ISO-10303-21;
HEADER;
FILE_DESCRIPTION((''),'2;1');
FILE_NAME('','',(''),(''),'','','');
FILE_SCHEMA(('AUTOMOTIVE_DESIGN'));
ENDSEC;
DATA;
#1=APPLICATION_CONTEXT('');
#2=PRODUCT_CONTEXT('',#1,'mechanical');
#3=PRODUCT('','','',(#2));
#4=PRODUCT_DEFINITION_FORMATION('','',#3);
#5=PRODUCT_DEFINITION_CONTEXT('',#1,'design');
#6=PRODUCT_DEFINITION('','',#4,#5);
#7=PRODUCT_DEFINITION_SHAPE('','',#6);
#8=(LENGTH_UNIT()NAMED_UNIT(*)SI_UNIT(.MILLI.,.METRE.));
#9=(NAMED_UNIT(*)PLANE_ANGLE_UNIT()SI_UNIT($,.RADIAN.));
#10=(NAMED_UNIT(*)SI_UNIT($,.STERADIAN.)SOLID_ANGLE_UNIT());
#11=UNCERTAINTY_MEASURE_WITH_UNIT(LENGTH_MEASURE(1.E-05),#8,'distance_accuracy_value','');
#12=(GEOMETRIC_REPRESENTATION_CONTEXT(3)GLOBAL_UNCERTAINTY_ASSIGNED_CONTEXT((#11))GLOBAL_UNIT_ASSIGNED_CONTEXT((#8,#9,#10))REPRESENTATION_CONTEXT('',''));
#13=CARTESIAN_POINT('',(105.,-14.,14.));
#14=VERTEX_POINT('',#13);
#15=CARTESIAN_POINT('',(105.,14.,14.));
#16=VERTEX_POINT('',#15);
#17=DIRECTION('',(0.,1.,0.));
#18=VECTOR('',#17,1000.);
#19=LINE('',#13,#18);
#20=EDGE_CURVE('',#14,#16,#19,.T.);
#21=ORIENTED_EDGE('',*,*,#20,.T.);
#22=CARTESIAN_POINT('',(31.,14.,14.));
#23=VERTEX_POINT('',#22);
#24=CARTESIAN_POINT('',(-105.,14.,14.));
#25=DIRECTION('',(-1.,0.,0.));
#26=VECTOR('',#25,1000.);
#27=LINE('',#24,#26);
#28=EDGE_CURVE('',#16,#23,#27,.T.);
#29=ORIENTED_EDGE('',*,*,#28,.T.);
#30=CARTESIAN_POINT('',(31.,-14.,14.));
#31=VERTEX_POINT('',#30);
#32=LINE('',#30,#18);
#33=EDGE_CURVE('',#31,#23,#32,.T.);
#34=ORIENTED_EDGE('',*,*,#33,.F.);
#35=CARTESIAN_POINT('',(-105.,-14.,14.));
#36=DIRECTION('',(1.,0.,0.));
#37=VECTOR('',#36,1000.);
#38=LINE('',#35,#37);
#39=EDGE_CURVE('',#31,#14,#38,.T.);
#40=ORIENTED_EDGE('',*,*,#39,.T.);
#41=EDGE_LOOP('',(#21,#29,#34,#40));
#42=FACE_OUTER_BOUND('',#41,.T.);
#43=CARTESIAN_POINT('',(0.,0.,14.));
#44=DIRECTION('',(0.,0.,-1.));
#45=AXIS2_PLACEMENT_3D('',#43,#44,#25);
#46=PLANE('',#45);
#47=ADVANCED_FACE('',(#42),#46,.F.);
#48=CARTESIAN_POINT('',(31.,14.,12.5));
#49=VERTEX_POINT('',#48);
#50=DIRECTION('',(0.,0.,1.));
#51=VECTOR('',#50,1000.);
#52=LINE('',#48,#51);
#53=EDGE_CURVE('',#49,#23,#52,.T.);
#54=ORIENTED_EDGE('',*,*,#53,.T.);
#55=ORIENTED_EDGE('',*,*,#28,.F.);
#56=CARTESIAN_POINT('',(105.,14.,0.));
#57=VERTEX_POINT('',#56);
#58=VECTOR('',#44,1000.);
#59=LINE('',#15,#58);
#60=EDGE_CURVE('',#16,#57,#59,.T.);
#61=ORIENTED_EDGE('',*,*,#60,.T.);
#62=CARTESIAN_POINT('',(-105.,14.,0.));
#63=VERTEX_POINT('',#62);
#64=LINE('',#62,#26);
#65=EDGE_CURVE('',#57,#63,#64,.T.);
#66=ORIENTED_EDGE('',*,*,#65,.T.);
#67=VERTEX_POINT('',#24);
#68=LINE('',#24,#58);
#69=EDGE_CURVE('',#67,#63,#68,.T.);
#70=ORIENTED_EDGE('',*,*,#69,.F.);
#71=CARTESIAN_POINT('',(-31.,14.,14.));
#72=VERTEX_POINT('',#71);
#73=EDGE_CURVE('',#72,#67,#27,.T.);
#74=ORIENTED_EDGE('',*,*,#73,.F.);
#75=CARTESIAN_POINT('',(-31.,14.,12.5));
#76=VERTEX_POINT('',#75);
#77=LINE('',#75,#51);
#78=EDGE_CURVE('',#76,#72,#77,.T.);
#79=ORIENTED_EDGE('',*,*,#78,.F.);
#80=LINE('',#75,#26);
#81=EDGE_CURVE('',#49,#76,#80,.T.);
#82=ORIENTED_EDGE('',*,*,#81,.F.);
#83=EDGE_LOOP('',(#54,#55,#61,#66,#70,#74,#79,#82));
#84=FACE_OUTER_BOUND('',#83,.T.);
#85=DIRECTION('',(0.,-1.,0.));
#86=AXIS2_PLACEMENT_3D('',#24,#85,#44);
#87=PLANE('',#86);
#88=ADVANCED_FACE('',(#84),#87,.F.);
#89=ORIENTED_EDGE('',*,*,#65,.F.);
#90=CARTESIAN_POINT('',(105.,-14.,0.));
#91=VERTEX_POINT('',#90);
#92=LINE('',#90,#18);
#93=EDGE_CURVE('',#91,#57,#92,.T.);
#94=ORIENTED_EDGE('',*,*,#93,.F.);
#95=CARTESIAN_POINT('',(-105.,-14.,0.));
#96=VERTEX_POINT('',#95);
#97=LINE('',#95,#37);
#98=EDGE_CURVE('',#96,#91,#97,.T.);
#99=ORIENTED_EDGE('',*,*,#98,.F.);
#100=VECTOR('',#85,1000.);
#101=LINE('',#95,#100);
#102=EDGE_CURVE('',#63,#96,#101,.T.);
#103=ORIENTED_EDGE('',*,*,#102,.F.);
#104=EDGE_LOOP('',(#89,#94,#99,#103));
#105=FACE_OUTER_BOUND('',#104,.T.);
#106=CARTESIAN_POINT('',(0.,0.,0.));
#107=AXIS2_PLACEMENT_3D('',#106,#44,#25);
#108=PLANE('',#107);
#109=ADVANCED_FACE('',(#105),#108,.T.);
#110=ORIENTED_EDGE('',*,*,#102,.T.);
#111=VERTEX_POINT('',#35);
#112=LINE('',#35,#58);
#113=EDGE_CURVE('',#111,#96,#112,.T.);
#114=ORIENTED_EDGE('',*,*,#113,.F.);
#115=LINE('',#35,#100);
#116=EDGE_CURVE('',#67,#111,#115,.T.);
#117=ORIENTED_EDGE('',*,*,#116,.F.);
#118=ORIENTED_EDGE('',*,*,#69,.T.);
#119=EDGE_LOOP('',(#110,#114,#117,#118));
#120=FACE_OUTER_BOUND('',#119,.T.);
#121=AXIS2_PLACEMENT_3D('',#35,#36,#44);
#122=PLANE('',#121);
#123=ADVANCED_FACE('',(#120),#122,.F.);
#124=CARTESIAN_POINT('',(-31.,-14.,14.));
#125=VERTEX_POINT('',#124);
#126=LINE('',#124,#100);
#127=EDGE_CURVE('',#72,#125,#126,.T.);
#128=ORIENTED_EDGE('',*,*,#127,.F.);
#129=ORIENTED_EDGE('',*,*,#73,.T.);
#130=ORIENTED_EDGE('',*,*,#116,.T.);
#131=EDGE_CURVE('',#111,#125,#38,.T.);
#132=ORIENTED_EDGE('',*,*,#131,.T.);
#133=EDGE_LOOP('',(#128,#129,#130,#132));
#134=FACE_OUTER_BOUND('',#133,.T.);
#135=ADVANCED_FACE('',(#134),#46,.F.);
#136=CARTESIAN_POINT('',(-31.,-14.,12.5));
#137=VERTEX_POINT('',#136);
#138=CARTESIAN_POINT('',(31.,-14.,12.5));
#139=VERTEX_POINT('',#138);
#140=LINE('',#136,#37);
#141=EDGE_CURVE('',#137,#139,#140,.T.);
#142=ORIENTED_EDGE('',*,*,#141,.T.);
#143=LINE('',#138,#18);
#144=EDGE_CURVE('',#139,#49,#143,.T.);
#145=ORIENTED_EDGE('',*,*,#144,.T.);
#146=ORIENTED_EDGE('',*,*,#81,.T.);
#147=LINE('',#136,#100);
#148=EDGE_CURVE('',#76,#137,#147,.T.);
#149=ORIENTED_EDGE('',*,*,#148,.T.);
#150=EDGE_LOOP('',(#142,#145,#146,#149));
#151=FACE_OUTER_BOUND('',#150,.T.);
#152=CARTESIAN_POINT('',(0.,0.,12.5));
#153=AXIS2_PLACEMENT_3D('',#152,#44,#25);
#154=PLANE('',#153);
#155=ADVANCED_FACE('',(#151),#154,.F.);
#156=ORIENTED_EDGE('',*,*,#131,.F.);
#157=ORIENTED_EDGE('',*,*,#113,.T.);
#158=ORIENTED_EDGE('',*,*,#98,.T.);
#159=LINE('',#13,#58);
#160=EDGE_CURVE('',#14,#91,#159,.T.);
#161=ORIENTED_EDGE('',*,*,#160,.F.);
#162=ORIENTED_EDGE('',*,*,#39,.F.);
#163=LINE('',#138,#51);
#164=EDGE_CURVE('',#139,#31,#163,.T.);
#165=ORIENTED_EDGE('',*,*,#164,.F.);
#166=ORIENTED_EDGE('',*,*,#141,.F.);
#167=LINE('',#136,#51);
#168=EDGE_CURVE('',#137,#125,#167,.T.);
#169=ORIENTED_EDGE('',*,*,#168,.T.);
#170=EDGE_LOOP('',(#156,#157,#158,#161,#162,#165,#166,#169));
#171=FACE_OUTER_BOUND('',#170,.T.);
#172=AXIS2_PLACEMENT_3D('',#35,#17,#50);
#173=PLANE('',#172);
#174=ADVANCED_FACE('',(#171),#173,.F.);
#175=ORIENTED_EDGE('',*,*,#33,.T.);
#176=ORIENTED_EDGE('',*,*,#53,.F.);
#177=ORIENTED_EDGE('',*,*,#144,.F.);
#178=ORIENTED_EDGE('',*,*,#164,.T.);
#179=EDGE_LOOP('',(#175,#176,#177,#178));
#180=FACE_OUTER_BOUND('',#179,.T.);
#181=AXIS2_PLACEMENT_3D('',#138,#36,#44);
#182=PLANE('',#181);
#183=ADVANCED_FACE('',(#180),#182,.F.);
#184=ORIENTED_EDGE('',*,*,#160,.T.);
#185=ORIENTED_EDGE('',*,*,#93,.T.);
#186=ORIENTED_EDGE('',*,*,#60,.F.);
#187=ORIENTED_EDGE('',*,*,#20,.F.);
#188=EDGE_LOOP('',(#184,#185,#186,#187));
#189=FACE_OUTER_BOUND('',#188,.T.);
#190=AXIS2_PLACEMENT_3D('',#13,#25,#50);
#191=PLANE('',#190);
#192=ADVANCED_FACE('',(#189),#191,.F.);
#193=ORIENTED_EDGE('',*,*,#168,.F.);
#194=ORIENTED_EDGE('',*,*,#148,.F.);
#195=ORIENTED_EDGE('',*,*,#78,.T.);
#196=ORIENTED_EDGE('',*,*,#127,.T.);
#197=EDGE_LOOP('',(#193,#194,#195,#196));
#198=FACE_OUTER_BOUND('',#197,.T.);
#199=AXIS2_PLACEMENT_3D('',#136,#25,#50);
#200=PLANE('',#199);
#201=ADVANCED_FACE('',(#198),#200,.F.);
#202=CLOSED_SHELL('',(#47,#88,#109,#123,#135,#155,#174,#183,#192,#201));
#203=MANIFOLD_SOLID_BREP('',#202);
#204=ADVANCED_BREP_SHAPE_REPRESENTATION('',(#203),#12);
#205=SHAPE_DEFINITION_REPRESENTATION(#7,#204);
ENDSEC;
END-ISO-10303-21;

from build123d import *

# Parameters (mm, degrees)
SKETCH_1_W          = 210
SKETCH_1_H          = 28
EXTRUDE_1_DEPTH     = 14
SKETCH_2_W          = 62
SKETCH_2_H          = 28
CUT_EXTRUDE_1_DEPTH = 1.5


with BuildPart() as part:
    # 草图1 → 凸台-拉伸1 (new body)
    with BuildSketch(Plane.XY):
        Rectangle(SKETCH_1_W, SKETCH_1_H)
    extrude(amount=EXTRUDE_1_DEPTH)

    # 草图2 → 切除-拉伸1 (cut)
    with BuildSketch(Plane.XY.offset(14)):
        Rectangle(SKETCH_2_W, SKETCH_2_H)
    extrude(amount=-CUT_EXTRUDE_1_DEPTH, mode=Mode.SUBTRACT)


solid = part.part
